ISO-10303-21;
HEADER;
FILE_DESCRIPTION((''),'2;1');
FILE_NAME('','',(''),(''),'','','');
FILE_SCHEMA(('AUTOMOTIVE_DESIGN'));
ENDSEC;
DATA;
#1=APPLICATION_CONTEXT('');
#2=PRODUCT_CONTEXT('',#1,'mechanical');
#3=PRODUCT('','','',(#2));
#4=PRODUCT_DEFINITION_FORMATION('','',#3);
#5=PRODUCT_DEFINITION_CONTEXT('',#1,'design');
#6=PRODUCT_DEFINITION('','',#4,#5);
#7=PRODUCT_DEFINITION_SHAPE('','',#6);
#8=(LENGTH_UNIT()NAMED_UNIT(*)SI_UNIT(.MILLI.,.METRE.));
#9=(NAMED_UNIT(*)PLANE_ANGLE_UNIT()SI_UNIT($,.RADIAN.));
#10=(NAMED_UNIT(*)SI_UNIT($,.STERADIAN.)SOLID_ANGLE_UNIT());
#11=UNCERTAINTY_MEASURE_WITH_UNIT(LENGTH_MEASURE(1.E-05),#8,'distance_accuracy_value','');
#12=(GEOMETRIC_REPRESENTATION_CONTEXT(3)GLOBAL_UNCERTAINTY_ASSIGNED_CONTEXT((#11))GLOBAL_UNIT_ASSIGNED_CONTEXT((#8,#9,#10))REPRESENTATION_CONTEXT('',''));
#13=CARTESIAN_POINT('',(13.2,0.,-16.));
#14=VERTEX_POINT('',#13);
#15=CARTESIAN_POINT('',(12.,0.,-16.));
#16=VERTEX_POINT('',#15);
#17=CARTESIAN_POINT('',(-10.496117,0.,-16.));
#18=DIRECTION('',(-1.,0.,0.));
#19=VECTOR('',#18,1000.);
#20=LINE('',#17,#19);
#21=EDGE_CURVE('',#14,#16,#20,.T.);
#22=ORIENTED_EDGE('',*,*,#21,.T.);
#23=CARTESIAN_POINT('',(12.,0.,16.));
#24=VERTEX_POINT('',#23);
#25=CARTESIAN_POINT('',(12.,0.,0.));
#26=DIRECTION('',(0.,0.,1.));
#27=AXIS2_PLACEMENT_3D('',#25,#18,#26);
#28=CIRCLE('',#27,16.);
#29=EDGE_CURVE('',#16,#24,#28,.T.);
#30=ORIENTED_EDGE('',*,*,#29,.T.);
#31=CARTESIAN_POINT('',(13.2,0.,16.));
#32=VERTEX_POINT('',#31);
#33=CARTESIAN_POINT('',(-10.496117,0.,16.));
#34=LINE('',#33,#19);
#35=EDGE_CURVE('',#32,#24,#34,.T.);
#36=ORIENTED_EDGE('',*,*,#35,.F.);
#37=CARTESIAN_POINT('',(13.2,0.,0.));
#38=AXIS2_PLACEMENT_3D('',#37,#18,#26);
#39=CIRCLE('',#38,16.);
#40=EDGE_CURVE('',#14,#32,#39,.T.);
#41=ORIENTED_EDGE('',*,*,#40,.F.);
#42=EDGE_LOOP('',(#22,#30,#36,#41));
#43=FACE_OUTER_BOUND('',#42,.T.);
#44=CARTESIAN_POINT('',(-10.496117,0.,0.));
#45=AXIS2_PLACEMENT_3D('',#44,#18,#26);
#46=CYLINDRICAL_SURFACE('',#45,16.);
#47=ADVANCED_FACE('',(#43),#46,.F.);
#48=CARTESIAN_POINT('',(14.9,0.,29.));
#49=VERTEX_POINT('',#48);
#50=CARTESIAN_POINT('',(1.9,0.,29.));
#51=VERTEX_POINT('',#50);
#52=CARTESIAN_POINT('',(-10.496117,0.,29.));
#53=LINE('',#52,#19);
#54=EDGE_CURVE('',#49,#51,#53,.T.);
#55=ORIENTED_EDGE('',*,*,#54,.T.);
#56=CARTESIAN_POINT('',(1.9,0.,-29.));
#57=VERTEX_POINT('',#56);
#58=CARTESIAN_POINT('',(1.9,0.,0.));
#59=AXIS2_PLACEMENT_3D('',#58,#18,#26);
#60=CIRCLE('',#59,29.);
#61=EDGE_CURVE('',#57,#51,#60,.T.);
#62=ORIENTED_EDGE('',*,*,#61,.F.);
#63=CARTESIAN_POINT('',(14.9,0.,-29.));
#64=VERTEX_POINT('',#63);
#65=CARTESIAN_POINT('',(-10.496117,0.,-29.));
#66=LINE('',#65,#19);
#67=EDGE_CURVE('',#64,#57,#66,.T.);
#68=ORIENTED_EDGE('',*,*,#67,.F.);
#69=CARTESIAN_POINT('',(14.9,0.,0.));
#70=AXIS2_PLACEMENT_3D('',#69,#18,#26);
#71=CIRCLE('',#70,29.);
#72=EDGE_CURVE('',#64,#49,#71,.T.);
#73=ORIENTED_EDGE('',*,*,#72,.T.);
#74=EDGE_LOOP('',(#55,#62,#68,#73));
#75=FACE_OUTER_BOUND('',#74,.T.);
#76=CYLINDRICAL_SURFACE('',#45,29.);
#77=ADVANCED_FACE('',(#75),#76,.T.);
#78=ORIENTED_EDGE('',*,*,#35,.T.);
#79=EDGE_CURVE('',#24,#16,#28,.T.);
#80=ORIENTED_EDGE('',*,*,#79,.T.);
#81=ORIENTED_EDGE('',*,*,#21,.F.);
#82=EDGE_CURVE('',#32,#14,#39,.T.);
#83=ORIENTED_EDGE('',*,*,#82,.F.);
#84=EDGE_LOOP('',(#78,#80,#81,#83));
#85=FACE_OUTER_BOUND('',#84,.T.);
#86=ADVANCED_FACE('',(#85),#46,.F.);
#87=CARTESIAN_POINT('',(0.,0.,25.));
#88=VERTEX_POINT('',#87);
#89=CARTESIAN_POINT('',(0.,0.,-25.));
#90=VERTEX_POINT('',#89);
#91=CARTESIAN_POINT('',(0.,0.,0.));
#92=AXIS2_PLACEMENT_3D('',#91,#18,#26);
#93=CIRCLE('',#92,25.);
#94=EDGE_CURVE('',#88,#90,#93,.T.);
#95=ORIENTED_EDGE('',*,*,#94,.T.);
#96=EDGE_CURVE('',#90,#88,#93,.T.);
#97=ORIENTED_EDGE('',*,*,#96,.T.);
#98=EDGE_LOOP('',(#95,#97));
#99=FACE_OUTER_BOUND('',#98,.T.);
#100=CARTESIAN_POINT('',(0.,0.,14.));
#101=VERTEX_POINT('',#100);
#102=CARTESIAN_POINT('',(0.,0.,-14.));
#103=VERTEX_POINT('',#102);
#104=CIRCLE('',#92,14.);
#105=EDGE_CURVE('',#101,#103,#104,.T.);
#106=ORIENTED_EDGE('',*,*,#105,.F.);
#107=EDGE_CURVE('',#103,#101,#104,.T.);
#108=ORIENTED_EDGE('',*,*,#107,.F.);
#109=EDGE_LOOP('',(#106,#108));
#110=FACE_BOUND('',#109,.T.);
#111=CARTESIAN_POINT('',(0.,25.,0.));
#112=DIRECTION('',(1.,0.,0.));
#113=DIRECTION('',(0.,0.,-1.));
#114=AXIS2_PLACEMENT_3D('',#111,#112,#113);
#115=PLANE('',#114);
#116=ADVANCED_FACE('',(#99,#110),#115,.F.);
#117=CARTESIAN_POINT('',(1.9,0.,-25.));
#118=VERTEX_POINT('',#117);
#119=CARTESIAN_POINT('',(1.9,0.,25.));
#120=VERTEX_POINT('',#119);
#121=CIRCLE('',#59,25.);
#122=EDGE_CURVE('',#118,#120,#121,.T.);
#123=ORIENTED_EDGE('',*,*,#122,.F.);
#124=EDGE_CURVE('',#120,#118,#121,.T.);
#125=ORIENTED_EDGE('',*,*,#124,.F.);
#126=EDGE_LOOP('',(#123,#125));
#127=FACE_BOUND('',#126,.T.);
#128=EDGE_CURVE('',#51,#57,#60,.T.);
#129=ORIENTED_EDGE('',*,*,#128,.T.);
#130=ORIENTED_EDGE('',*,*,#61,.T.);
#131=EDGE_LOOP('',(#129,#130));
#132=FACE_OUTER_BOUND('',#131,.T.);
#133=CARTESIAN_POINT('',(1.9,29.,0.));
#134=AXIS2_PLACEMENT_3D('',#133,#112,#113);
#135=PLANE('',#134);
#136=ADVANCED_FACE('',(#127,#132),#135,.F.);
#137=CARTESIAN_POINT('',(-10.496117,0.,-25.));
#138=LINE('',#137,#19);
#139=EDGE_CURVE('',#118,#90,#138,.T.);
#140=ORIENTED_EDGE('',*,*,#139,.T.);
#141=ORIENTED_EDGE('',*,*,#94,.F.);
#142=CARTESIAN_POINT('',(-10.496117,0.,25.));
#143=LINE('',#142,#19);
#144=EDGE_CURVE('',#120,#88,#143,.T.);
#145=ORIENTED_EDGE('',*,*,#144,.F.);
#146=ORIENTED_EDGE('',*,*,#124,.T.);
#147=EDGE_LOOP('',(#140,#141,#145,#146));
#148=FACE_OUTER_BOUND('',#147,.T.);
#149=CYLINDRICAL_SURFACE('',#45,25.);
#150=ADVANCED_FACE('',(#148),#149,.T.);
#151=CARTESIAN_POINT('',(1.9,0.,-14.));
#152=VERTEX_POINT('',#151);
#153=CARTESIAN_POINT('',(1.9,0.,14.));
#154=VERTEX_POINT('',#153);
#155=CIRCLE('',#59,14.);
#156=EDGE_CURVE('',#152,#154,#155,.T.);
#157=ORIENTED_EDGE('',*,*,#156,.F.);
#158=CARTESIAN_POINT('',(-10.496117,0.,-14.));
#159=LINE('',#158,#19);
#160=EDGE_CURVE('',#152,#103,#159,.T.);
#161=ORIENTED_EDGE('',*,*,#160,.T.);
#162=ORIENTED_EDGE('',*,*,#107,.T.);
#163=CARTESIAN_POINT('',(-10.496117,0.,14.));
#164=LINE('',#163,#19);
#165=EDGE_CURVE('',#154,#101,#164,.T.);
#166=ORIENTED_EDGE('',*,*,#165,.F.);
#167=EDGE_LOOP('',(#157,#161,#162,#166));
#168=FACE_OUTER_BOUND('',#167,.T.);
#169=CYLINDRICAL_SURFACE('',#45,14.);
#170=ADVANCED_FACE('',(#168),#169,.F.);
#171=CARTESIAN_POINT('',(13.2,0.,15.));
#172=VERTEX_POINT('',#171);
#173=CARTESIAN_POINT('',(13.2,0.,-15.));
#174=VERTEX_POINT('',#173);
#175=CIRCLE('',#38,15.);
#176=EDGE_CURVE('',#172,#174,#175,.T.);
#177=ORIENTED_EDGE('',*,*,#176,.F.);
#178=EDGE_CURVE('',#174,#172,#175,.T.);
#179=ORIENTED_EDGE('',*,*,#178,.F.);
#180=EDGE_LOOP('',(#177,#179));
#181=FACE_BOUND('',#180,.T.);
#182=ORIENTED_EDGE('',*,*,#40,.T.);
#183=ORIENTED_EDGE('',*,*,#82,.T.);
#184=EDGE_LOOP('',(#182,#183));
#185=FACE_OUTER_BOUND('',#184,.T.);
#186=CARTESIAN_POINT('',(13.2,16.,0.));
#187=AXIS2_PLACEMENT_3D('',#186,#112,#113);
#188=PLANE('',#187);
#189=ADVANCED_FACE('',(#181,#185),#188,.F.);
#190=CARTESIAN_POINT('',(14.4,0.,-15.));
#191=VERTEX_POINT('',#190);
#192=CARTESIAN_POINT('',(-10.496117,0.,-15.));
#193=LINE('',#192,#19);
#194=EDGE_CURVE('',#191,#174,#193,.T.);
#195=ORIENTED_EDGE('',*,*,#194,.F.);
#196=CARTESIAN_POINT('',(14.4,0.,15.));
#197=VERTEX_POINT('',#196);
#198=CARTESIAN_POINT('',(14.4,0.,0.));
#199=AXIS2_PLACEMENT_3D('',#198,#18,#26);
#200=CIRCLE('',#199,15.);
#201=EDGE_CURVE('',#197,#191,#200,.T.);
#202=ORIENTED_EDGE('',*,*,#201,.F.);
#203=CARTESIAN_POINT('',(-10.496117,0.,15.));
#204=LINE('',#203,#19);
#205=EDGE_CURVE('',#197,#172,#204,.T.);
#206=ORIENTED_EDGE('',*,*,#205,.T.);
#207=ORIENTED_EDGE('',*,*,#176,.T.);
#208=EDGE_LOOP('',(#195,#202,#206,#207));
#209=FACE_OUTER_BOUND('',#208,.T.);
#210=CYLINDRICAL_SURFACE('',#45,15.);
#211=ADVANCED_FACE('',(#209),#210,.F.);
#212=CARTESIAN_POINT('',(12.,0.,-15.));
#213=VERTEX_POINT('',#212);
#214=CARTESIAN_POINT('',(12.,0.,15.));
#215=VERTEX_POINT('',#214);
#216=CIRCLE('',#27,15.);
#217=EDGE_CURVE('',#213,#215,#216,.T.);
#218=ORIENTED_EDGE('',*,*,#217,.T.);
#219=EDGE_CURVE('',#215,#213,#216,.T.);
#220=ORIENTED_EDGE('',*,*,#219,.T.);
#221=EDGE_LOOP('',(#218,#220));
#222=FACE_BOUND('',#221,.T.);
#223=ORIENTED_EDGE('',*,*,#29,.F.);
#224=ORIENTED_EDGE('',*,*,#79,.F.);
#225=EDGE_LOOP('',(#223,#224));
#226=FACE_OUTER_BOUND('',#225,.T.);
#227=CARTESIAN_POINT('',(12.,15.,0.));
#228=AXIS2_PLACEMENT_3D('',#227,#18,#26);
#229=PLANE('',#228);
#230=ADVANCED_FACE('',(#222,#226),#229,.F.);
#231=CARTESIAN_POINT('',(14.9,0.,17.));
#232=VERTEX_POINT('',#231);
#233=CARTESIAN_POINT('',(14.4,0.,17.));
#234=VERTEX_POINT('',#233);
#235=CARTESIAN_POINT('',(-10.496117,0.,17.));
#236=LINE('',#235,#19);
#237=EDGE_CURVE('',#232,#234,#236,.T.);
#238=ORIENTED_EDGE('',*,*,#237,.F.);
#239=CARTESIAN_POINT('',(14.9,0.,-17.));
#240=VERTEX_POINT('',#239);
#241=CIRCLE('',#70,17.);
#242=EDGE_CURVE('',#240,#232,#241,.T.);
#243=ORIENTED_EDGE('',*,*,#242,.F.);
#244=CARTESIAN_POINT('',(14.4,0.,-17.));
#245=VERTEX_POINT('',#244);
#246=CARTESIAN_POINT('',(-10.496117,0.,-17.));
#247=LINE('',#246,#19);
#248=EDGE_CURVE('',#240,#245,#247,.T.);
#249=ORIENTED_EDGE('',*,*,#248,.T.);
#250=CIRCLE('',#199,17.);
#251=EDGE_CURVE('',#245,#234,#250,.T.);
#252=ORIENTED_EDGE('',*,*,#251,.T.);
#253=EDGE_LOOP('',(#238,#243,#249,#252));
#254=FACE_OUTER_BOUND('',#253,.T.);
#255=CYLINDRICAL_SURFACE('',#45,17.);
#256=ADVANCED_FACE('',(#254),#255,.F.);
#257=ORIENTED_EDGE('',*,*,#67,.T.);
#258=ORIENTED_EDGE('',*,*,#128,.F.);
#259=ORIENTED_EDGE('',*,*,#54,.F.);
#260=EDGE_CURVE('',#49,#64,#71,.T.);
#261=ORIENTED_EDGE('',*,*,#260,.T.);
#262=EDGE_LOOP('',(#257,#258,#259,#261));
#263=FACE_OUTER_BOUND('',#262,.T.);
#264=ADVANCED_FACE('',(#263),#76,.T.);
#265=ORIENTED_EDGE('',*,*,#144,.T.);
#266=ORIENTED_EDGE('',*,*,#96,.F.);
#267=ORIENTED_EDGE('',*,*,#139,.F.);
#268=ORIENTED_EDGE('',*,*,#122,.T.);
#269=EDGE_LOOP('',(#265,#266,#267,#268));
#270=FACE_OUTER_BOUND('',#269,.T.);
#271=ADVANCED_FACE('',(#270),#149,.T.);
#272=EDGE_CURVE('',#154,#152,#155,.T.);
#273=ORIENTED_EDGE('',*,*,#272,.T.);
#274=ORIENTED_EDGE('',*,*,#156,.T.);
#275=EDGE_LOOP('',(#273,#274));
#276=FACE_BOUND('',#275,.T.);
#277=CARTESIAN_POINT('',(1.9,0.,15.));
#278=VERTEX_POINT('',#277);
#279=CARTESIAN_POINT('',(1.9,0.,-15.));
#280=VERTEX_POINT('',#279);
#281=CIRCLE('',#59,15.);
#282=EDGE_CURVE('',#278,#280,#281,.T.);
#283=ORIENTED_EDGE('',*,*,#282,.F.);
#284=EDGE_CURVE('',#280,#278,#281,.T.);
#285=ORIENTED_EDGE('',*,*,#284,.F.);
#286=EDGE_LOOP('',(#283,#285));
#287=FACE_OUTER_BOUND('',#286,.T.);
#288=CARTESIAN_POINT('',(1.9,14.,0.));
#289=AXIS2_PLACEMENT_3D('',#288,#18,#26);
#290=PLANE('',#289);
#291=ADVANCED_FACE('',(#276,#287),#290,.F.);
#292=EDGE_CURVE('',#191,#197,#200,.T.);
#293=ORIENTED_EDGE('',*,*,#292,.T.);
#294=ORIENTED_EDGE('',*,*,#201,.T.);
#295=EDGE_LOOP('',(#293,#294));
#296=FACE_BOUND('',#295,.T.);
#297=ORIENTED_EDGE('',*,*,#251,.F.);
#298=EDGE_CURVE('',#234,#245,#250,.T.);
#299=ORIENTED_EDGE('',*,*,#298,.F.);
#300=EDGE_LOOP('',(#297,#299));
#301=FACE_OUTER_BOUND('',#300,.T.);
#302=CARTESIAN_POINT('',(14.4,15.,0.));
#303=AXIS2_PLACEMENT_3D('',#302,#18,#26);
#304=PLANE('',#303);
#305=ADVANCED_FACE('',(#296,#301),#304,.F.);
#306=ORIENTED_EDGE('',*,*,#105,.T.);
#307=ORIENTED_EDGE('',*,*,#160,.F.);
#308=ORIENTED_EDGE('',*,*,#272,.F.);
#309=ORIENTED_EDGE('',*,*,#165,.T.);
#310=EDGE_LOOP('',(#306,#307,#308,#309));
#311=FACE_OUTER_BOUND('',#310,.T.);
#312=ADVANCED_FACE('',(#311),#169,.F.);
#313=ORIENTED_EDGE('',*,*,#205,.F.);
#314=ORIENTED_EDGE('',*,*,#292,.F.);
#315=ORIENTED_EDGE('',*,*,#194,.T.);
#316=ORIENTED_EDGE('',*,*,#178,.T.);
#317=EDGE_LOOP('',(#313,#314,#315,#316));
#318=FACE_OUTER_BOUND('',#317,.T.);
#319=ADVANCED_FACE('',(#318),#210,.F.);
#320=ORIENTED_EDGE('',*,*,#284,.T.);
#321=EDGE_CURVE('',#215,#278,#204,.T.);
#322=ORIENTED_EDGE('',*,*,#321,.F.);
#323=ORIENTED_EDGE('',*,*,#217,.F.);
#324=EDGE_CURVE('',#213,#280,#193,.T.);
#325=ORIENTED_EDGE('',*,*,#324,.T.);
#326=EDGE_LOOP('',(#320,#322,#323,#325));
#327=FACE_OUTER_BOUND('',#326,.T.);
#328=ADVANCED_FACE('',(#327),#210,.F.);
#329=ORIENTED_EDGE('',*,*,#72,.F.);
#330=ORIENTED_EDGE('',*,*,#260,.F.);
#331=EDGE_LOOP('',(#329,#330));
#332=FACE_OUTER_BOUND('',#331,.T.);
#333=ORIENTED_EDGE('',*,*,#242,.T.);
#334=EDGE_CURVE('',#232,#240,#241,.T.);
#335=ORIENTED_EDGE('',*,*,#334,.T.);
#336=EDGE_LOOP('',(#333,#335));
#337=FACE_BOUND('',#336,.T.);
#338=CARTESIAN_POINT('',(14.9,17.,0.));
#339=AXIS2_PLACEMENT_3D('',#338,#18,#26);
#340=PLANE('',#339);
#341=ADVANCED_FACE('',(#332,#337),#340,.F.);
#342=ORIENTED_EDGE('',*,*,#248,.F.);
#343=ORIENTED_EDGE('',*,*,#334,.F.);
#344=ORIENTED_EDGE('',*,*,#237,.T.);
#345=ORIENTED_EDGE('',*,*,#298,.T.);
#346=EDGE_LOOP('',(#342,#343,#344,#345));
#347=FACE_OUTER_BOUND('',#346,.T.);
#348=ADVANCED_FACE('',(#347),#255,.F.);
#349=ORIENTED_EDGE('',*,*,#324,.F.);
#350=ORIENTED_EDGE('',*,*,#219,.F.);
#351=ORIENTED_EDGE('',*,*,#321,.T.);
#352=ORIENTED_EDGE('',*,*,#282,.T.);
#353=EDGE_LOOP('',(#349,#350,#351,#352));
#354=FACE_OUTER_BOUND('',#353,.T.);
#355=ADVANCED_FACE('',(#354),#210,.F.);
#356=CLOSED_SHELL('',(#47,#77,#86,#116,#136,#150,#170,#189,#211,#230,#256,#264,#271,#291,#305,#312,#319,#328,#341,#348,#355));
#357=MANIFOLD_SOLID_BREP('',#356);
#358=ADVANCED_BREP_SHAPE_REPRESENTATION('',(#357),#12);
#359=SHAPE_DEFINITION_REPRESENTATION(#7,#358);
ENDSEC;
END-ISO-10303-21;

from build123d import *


with BuildPart() as part:
    # 草图2 → 旋转1 (revolve)
    with BuildSketch(Plane.XY, mode=Mode.PRIVATE) as revolve_1_sk:
        Polygon((0, 14), (1.9, 14), (1.9, 15), (12, 15), (12, 16), (13.2, 16), (13.2, 15), (14.4, 15), (14.4, 17), (14.9, 17), (14.9, 29), (1.9, 29), (1.9, 25), (0, 25), align=None)
    revolve(revolve_1_sk.sketch.rotate(Axis((-10.496116508, 0, 0), (1, 0, 0)), 90), axis=Axis((-10.496116508, 0, 0), (1, 0, 0)))


solid = part.part
